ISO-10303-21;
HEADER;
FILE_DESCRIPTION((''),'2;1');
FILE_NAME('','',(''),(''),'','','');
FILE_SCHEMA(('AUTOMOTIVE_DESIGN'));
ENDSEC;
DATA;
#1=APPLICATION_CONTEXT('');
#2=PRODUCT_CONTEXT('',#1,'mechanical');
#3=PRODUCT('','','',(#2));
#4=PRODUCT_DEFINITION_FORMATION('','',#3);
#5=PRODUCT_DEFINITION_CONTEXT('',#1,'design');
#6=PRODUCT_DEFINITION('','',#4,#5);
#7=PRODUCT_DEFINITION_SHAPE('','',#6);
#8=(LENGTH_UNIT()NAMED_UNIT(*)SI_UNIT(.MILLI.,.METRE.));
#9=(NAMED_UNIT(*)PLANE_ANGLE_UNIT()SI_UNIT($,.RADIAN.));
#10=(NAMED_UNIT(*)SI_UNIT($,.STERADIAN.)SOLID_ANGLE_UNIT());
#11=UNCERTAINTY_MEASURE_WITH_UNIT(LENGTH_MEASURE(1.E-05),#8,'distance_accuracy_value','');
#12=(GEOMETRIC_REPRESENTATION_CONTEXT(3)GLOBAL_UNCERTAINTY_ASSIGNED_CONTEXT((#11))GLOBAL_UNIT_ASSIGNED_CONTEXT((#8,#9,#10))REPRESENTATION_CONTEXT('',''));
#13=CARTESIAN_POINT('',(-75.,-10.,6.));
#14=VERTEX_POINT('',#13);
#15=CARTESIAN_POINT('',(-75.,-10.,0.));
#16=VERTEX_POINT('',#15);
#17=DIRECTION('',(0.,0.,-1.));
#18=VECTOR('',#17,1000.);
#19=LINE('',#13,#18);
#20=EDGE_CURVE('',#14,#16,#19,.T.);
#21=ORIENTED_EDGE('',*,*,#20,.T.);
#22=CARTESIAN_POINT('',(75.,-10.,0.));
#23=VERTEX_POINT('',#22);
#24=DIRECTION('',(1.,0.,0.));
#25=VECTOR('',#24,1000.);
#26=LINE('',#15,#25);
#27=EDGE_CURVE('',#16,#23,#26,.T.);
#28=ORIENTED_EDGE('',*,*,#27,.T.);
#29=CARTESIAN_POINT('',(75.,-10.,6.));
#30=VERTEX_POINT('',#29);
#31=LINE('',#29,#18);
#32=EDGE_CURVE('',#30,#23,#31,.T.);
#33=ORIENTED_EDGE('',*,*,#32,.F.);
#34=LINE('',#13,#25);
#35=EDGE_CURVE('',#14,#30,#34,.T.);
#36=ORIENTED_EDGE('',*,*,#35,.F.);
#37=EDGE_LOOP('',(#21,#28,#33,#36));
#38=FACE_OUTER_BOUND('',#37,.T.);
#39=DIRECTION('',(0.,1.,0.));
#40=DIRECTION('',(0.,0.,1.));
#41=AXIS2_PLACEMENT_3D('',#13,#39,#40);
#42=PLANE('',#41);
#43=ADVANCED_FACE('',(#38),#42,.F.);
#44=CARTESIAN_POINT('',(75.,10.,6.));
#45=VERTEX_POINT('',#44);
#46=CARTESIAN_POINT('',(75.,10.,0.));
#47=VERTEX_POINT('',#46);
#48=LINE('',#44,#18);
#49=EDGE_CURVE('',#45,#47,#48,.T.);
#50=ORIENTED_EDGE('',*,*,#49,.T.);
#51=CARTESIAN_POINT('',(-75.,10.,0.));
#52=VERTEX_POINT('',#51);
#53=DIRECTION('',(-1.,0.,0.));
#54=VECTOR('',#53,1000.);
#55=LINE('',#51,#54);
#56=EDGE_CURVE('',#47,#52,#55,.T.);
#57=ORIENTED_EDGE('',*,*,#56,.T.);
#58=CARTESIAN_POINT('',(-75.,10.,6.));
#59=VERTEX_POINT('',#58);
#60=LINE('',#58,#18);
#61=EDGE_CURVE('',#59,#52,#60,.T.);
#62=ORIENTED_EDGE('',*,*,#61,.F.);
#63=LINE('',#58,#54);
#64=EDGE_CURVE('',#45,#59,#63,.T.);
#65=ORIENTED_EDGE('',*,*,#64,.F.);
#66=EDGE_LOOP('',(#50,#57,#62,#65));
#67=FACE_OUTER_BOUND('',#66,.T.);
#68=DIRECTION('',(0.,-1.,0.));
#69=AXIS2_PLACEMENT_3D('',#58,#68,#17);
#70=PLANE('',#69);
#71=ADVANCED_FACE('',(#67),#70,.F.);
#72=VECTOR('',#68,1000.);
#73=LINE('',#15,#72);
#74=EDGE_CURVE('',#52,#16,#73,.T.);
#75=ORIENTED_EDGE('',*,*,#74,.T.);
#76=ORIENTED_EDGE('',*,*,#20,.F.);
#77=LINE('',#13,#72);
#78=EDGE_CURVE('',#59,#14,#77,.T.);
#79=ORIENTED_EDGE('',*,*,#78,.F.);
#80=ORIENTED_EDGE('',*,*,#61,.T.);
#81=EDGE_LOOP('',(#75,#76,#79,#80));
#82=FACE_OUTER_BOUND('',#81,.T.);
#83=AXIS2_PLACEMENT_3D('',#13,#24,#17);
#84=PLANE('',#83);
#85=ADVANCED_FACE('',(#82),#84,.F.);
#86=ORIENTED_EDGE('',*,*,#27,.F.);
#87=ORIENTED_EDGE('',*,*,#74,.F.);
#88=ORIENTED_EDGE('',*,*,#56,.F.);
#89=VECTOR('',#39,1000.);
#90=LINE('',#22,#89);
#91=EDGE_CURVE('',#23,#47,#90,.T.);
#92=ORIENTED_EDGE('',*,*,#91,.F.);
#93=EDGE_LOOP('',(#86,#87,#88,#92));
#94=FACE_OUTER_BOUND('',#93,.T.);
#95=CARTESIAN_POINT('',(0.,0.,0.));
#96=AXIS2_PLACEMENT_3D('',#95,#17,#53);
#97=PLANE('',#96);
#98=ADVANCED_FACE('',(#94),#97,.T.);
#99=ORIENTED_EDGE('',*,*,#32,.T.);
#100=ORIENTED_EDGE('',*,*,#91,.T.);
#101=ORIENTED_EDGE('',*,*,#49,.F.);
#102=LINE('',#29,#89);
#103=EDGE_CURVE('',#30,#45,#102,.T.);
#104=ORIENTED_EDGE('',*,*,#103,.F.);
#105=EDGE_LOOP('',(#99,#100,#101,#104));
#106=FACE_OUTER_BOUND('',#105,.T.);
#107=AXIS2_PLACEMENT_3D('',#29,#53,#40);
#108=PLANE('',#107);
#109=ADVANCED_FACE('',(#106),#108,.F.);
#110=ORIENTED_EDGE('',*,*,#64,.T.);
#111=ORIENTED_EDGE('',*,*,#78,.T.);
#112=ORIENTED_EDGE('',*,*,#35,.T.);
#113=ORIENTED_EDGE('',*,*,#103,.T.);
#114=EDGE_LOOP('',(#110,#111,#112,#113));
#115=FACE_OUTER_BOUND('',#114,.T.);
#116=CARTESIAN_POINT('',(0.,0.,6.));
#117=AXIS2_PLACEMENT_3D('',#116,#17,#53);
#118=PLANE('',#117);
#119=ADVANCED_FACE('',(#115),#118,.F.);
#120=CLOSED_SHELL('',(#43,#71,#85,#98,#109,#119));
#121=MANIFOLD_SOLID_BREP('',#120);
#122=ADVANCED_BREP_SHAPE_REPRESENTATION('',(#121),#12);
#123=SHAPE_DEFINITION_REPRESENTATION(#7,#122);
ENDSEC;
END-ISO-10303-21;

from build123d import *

# Parameters (mm, degrees)
SKETCH_1_W      = 150
SKETCH_1_H      = 20
EXTRUDE_1_DEPTH = 6


with BuildPart() as part:
    # 草图1 → 凸台-拉伸1 (new body)
    with BuildSketch(Plane.XY):
        Rectangle(SKETCH_1_W, SKETCH_1_H)
    extrude(amount=EXTRUDE_1_DEPTH)


solid = part.part
